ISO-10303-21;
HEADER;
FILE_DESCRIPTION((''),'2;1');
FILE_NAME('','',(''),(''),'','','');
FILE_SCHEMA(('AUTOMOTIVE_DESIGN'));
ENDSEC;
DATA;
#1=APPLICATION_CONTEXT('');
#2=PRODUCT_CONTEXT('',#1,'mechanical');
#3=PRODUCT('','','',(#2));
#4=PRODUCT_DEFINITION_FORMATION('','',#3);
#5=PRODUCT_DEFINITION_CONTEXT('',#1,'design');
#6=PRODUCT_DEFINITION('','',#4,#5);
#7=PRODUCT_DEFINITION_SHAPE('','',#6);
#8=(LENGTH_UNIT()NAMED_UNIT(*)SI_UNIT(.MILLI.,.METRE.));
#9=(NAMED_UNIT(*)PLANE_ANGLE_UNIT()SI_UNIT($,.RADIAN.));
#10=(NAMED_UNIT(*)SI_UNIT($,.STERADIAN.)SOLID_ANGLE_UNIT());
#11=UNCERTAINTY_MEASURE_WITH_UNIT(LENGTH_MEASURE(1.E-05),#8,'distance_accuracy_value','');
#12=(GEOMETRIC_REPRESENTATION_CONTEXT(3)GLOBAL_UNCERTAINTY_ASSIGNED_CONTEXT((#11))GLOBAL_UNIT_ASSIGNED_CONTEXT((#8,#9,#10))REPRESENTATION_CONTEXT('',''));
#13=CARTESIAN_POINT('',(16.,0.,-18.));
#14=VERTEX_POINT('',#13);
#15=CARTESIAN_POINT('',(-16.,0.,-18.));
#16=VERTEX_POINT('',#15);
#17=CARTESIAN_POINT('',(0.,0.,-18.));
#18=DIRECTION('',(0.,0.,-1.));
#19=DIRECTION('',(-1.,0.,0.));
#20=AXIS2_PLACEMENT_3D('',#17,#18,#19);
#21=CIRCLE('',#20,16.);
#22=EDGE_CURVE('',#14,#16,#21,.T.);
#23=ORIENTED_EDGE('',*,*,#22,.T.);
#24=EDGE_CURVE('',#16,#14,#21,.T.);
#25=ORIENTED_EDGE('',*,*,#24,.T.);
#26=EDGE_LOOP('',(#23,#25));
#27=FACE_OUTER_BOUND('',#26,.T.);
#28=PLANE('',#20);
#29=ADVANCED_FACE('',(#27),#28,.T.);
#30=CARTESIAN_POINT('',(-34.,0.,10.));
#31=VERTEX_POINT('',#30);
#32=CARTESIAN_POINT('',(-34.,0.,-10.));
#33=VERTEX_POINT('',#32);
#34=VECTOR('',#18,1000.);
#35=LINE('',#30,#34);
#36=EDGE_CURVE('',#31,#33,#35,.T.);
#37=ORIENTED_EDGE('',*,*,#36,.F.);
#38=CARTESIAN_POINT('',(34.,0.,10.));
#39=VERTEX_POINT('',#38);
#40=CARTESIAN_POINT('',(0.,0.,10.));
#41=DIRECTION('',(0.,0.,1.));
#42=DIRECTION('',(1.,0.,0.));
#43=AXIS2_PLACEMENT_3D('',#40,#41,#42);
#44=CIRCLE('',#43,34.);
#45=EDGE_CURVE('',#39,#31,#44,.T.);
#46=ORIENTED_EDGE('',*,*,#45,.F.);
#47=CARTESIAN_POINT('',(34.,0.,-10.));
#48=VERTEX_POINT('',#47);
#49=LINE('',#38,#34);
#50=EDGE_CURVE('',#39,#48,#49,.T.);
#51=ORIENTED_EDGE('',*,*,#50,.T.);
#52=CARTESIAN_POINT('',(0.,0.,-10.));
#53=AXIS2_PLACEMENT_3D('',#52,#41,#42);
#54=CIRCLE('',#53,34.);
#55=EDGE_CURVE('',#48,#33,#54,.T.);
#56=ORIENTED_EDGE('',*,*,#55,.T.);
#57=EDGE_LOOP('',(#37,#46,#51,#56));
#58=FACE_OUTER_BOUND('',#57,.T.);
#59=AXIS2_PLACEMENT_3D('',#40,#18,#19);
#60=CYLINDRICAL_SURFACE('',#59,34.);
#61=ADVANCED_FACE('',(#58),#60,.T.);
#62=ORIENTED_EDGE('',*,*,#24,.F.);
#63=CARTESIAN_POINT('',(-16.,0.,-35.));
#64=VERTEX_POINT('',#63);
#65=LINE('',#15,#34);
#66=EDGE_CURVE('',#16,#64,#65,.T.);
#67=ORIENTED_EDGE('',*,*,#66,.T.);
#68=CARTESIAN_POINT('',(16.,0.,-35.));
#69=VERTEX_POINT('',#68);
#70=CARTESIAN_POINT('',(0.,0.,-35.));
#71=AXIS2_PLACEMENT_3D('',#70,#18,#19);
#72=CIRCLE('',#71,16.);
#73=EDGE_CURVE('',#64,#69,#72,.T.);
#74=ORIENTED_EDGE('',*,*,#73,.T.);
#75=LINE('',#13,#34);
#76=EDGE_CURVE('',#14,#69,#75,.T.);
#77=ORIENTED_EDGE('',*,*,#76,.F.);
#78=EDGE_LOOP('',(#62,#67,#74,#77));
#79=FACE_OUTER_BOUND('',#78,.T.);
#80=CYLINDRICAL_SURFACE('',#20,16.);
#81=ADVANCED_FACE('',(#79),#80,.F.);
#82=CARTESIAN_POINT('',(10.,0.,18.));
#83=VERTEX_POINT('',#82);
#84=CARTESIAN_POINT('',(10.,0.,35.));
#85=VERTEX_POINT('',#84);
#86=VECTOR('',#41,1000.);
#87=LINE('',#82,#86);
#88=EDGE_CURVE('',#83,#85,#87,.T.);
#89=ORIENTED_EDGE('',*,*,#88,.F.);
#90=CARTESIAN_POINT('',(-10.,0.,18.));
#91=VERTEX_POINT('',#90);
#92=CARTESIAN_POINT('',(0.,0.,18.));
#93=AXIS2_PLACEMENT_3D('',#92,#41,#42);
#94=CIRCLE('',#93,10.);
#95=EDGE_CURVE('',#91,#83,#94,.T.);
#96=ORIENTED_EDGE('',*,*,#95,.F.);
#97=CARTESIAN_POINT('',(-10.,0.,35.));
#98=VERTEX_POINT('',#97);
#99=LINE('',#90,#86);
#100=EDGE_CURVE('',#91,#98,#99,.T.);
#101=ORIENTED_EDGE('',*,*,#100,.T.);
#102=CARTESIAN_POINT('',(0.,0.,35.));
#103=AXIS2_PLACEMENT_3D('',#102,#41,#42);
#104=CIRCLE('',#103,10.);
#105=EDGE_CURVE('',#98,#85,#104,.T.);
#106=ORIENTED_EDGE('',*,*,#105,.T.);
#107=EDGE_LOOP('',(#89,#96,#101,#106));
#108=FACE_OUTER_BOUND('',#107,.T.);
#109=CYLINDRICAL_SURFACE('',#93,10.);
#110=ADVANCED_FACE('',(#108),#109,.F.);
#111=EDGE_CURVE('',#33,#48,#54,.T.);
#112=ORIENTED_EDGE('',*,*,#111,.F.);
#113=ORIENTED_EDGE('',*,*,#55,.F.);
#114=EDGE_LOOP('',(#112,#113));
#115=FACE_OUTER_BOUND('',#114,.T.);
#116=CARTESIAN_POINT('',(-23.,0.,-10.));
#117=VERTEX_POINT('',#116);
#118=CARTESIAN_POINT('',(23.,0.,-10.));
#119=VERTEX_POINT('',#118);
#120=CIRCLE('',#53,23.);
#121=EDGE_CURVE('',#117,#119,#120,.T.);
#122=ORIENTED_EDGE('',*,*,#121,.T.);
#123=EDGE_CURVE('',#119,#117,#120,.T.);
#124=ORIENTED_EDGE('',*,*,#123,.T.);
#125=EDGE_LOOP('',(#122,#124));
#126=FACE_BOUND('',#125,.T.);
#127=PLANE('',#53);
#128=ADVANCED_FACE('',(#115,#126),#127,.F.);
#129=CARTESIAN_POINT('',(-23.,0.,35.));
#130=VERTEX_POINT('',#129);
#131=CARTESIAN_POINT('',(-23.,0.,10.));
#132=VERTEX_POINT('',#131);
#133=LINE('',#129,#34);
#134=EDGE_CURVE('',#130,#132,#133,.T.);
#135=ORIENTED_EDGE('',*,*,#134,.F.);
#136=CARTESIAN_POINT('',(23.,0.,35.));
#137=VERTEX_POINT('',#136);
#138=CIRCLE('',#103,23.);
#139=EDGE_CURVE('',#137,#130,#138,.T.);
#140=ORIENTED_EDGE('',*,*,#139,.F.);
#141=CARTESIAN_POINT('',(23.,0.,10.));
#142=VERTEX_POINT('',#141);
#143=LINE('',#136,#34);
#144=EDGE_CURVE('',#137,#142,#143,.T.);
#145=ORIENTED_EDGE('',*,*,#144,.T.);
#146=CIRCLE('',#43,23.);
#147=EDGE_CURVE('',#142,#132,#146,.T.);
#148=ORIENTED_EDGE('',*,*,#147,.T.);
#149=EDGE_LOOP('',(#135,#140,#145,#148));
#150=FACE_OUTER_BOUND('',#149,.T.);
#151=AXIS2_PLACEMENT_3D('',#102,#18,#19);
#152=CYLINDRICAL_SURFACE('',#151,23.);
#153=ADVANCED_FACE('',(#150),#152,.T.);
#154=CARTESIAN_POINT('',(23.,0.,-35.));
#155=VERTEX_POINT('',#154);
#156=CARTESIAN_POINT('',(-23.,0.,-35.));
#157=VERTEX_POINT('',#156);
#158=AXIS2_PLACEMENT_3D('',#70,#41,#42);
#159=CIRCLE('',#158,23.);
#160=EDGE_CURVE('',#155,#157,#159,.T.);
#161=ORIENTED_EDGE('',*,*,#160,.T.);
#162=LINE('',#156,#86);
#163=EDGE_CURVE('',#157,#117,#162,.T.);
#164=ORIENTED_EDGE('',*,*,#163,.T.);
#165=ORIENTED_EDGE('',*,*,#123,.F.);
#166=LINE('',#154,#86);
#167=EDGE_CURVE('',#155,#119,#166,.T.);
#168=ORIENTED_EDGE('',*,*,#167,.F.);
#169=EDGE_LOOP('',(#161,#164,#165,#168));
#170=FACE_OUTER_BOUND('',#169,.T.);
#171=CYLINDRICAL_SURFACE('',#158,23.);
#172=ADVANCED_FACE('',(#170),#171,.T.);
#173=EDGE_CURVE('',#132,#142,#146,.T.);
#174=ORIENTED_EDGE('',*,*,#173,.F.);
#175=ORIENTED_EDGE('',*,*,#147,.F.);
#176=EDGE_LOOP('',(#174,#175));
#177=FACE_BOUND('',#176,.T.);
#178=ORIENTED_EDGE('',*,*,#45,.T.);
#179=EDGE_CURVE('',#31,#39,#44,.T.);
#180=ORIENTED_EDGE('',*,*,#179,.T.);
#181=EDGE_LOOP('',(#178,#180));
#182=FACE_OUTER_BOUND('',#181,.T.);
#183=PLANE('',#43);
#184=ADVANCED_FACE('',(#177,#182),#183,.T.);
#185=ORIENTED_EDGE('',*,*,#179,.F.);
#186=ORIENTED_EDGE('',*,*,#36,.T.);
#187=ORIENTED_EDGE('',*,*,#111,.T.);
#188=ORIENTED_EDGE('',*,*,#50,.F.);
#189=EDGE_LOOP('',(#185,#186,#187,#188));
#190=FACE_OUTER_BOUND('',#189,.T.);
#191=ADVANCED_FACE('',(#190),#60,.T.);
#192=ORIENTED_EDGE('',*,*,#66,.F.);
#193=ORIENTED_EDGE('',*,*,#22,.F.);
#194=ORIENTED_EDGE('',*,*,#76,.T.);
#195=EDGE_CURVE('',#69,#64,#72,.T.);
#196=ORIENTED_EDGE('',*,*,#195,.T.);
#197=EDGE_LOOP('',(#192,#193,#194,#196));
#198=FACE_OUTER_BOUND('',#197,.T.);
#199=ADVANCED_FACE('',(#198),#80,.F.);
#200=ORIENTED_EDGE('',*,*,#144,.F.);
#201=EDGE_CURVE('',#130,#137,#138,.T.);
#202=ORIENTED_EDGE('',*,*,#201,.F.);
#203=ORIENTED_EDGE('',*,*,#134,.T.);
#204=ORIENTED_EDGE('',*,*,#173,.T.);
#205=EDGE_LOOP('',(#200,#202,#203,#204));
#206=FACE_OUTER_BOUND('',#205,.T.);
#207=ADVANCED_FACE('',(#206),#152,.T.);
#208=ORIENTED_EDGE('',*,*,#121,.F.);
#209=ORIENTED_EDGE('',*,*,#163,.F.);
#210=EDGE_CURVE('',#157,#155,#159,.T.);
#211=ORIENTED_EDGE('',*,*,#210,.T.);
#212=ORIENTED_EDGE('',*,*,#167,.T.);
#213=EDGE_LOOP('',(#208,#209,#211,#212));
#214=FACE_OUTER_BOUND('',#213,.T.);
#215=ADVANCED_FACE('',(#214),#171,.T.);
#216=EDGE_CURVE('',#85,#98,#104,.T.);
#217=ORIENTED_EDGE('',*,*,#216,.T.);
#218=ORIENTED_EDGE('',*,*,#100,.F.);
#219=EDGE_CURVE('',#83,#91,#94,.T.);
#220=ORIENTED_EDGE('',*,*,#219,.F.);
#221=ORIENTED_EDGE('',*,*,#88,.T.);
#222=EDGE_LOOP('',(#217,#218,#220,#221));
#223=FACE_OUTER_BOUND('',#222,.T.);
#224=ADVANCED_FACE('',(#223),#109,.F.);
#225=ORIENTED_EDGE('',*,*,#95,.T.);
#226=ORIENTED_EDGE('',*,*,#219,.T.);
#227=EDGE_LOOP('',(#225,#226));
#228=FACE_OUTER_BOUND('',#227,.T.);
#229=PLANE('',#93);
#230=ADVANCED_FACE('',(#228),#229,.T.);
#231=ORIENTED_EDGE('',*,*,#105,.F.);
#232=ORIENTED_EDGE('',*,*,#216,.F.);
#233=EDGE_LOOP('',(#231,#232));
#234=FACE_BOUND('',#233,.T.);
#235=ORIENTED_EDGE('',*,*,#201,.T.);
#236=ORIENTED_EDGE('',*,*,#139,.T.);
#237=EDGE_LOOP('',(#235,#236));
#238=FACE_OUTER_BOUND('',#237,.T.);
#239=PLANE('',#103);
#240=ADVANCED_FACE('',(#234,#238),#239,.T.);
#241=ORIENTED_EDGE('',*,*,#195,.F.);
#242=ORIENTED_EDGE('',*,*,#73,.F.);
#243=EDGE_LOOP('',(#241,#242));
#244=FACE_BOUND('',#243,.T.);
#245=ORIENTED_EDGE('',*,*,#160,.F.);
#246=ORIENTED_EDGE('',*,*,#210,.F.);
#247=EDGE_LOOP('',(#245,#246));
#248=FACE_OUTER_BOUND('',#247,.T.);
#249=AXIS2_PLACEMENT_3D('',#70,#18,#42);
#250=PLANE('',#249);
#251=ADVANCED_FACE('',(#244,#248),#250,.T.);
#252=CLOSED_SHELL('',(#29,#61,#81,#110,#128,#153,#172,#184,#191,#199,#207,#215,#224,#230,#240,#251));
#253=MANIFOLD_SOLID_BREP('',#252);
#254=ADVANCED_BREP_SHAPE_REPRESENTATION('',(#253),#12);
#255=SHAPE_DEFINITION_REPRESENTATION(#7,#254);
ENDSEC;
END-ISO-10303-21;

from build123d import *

# Parameters (mm, degrees)
SKETCH1_R           = 34
BOSS_EXTRUDE1_DEPTH = 10
SKETCH2_R           = 23
BOSS_EXTRUDE2_DEPTH = 25
SKETCH3_R           = 10
CUT_EXTRUDE1_DEPTH  = 17
SKETCH4_R           = 16
CUT_EXTRUDE2_DEPTH  = 17


with BuildPart() as part:
    # Sketch1 → Boss-Extrude1 (new, symmetric)
    with BuildSketch(Plane.XY):
        Circle(SKETCH1_R)
    extrude(amount=BOSS_EXTRUDE1_DEPTH, both=True)

    # Sketch2 → Boss-Extrude2 (add)
    with BuildSketch(Plane.XY.offset(10)):
        Circle(SKETCH2_R)
    boss_extrude2 = extrude(amount=BOSS_EXTRUDE2_DEPTH)

    # Mirror1: Boss-Extrude2 across plane
    add(boss_extrude2.mirror(Plane.XY))

    # Sketch3 → Cut-Extrude1 (cut)
    with BuildSketch(Plane.XY.offset(35)):
        Circle(SKETCH3_R)
    extrude(amount=-CUT_EXTRUDE1_DEPTH, mode=Mode.SUBTRACT)

    # Sketch4 → Cut-Extrude2 (cut)
    with BuildSketch(Plane(origin=(0, 0, -35), x_dir=(-1, 0, 0), z_dir=(0, 0, -1))):
        Circle(SKETCH4_R)
    extrude(amount=-CUT_EXTRUDE2_DEPTH, mode=Mode.SUBTRACT)


solid = part.part
